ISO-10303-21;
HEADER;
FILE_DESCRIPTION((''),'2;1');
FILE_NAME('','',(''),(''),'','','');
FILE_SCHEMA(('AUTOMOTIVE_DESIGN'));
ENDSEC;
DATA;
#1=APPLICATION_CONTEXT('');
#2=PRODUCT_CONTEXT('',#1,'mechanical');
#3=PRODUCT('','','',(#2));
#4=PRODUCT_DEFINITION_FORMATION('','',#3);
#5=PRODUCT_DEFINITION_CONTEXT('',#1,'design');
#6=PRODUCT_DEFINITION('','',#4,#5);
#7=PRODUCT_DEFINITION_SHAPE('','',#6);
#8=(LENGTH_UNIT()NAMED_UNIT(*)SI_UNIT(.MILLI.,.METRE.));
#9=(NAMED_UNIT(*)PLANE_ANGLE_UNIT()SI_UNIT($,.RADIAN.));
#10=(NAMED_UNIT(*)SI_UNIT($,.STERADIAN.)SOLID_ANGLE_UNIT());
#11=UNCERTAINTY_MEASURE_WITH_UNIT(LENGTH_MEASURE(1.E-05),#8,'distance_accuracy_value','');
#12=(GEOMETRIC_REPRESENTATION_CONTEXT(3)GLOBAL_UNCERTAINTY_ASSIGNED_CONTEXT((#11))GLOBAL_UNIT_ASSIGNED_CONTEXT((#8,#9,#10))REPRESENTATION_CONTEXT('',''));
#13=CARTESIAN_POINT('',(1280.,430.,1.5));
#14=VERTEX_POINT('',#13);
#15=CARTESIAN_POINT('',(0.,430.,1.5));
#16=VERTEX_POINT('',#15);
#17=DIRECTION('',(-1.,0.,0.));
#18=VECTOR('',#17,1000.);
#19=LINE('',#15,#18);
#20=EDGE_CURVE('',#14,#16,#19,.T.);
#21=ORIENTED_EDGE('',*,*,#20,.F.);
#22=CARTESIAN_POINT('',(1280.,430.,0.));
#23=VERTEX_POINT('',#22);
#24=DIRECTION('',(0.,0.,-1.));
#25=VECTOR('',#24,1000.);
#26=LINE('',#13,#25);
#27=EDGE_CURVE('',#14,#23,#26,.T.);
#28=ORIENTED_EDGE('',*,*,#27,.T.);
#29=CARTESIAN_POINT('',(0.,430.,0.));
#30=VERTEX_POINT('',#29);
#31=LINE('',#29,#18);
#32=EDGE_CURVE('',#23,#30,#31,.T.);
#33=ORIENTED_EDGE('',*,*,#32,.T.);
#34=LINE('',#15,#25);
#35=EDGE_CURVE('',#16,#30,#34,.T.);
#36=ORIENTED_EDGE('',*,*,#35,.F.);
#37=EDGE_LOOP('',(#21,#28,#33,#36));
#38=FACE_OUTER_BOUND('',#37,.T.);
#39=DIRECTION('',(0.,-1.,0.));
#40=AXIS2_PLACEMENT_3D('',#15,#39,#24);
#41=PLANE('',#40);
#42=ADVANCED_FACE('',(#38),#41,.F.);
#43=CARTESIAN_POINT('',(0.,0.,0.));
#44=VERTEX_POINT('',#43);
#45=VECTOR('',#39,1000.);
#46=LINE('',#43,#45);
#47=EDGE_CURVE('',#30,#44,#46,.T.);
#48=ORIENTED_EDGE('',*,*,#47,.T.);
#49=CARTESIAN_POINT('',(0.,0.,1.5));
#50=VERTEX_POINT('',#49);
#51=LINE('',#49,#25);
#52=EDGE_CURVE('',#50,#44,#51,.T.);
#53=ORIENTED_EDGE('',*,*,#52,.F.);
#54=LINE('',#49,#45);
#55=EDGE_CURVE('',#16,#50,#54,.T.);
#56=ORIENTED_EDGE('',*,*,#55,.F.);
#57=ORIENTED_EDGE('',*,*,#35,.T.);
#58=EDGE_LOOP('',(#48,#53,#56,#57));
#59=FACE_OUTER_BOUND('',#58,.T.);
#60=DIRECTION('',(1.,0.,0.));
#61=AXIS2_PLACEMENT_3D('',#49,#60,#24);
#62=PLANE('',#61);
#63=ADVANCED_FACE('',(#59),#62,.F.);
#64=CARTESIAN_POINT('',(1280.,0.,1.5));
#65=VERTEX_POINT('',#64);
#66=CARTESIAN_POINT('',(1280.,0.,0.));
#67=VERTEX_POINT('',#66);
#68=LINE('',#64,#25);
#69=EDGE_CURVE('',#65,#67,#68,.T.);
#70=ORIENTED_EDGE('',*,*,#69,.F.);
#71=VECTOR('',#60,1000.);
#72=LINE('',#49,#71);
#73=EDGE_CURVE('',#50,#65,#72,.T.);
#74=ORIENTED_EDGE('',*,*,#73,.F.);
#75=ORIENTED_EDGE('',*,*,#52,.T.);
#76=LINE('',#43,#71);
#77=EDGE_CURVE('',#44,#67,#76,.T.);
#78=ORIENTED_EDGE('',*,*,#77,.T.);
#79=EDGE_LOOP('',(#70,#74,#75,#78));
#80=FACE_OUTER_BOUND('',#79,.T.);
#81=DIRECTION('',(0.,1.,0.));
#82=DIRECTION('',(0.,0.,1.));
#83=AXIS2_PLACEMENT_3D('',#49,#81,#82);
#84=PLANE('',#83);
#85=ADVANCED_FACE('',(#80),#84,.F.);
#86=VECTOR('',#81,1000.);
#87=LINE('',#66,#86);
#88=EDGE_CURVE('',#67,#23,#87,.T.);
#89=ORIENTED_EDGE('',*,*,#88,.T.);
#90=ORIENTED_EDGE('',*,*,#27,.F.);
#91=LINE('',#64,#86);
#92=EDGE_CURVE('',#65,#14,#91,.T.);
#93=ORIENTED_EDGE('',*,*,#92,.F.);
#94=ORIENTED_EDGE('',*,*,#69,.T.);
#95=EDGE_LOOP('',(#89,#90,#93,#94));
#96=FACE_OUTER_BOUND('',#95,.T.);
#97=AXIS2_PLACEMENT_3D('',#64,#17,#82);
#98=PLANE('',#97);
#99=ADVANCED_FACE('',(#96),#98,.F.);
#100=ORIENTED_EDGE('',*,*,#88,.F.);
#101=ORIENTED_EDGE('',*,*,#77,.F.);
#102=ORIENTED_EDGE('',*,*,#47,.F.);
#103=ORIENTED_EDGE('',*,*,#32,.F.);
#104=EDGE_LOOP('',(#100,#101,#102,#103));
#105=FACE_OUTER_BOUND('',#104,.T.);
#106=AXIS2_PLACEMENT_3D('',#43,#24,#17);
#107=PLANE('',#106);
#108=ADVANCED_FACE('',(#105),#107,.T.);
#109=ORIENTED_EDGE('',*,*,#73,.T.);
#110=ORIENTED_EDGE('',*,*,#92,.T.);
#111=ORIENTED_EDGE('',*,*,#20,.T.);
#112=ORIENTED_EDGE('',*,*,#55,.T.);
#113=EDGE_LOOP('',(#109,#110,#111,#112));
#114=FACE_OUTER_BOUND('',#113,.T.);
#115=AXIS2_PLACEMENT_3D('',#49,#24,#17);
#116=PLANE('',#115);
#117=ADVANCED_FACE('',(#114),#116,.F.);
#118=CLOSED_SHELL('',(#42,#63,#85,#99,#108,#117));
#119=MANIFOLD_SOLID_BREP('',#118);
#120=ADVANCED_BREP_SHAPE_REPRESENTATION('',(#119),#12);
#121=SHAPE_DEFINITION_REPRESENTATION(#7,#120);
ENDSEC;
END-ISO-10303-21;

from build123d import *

# Parameters (mm, degrees)
SKETCH1_W           = 1280
SKETCH1_H           = 430
BOSS_EXTRUDE1_DEPTH = 1.5


with BuildPart() as part:
    # Sketch1 → Boss-Extrude1 (new body)
    with BuildSketch(Plane.XY):
        with Locations((640, 215)):
            Rectangle(SKETCH1_W, SKETCH1_H)
    extrude(amount=BOSS_EXTRUDE1_DEPTH)


solid = part.part
